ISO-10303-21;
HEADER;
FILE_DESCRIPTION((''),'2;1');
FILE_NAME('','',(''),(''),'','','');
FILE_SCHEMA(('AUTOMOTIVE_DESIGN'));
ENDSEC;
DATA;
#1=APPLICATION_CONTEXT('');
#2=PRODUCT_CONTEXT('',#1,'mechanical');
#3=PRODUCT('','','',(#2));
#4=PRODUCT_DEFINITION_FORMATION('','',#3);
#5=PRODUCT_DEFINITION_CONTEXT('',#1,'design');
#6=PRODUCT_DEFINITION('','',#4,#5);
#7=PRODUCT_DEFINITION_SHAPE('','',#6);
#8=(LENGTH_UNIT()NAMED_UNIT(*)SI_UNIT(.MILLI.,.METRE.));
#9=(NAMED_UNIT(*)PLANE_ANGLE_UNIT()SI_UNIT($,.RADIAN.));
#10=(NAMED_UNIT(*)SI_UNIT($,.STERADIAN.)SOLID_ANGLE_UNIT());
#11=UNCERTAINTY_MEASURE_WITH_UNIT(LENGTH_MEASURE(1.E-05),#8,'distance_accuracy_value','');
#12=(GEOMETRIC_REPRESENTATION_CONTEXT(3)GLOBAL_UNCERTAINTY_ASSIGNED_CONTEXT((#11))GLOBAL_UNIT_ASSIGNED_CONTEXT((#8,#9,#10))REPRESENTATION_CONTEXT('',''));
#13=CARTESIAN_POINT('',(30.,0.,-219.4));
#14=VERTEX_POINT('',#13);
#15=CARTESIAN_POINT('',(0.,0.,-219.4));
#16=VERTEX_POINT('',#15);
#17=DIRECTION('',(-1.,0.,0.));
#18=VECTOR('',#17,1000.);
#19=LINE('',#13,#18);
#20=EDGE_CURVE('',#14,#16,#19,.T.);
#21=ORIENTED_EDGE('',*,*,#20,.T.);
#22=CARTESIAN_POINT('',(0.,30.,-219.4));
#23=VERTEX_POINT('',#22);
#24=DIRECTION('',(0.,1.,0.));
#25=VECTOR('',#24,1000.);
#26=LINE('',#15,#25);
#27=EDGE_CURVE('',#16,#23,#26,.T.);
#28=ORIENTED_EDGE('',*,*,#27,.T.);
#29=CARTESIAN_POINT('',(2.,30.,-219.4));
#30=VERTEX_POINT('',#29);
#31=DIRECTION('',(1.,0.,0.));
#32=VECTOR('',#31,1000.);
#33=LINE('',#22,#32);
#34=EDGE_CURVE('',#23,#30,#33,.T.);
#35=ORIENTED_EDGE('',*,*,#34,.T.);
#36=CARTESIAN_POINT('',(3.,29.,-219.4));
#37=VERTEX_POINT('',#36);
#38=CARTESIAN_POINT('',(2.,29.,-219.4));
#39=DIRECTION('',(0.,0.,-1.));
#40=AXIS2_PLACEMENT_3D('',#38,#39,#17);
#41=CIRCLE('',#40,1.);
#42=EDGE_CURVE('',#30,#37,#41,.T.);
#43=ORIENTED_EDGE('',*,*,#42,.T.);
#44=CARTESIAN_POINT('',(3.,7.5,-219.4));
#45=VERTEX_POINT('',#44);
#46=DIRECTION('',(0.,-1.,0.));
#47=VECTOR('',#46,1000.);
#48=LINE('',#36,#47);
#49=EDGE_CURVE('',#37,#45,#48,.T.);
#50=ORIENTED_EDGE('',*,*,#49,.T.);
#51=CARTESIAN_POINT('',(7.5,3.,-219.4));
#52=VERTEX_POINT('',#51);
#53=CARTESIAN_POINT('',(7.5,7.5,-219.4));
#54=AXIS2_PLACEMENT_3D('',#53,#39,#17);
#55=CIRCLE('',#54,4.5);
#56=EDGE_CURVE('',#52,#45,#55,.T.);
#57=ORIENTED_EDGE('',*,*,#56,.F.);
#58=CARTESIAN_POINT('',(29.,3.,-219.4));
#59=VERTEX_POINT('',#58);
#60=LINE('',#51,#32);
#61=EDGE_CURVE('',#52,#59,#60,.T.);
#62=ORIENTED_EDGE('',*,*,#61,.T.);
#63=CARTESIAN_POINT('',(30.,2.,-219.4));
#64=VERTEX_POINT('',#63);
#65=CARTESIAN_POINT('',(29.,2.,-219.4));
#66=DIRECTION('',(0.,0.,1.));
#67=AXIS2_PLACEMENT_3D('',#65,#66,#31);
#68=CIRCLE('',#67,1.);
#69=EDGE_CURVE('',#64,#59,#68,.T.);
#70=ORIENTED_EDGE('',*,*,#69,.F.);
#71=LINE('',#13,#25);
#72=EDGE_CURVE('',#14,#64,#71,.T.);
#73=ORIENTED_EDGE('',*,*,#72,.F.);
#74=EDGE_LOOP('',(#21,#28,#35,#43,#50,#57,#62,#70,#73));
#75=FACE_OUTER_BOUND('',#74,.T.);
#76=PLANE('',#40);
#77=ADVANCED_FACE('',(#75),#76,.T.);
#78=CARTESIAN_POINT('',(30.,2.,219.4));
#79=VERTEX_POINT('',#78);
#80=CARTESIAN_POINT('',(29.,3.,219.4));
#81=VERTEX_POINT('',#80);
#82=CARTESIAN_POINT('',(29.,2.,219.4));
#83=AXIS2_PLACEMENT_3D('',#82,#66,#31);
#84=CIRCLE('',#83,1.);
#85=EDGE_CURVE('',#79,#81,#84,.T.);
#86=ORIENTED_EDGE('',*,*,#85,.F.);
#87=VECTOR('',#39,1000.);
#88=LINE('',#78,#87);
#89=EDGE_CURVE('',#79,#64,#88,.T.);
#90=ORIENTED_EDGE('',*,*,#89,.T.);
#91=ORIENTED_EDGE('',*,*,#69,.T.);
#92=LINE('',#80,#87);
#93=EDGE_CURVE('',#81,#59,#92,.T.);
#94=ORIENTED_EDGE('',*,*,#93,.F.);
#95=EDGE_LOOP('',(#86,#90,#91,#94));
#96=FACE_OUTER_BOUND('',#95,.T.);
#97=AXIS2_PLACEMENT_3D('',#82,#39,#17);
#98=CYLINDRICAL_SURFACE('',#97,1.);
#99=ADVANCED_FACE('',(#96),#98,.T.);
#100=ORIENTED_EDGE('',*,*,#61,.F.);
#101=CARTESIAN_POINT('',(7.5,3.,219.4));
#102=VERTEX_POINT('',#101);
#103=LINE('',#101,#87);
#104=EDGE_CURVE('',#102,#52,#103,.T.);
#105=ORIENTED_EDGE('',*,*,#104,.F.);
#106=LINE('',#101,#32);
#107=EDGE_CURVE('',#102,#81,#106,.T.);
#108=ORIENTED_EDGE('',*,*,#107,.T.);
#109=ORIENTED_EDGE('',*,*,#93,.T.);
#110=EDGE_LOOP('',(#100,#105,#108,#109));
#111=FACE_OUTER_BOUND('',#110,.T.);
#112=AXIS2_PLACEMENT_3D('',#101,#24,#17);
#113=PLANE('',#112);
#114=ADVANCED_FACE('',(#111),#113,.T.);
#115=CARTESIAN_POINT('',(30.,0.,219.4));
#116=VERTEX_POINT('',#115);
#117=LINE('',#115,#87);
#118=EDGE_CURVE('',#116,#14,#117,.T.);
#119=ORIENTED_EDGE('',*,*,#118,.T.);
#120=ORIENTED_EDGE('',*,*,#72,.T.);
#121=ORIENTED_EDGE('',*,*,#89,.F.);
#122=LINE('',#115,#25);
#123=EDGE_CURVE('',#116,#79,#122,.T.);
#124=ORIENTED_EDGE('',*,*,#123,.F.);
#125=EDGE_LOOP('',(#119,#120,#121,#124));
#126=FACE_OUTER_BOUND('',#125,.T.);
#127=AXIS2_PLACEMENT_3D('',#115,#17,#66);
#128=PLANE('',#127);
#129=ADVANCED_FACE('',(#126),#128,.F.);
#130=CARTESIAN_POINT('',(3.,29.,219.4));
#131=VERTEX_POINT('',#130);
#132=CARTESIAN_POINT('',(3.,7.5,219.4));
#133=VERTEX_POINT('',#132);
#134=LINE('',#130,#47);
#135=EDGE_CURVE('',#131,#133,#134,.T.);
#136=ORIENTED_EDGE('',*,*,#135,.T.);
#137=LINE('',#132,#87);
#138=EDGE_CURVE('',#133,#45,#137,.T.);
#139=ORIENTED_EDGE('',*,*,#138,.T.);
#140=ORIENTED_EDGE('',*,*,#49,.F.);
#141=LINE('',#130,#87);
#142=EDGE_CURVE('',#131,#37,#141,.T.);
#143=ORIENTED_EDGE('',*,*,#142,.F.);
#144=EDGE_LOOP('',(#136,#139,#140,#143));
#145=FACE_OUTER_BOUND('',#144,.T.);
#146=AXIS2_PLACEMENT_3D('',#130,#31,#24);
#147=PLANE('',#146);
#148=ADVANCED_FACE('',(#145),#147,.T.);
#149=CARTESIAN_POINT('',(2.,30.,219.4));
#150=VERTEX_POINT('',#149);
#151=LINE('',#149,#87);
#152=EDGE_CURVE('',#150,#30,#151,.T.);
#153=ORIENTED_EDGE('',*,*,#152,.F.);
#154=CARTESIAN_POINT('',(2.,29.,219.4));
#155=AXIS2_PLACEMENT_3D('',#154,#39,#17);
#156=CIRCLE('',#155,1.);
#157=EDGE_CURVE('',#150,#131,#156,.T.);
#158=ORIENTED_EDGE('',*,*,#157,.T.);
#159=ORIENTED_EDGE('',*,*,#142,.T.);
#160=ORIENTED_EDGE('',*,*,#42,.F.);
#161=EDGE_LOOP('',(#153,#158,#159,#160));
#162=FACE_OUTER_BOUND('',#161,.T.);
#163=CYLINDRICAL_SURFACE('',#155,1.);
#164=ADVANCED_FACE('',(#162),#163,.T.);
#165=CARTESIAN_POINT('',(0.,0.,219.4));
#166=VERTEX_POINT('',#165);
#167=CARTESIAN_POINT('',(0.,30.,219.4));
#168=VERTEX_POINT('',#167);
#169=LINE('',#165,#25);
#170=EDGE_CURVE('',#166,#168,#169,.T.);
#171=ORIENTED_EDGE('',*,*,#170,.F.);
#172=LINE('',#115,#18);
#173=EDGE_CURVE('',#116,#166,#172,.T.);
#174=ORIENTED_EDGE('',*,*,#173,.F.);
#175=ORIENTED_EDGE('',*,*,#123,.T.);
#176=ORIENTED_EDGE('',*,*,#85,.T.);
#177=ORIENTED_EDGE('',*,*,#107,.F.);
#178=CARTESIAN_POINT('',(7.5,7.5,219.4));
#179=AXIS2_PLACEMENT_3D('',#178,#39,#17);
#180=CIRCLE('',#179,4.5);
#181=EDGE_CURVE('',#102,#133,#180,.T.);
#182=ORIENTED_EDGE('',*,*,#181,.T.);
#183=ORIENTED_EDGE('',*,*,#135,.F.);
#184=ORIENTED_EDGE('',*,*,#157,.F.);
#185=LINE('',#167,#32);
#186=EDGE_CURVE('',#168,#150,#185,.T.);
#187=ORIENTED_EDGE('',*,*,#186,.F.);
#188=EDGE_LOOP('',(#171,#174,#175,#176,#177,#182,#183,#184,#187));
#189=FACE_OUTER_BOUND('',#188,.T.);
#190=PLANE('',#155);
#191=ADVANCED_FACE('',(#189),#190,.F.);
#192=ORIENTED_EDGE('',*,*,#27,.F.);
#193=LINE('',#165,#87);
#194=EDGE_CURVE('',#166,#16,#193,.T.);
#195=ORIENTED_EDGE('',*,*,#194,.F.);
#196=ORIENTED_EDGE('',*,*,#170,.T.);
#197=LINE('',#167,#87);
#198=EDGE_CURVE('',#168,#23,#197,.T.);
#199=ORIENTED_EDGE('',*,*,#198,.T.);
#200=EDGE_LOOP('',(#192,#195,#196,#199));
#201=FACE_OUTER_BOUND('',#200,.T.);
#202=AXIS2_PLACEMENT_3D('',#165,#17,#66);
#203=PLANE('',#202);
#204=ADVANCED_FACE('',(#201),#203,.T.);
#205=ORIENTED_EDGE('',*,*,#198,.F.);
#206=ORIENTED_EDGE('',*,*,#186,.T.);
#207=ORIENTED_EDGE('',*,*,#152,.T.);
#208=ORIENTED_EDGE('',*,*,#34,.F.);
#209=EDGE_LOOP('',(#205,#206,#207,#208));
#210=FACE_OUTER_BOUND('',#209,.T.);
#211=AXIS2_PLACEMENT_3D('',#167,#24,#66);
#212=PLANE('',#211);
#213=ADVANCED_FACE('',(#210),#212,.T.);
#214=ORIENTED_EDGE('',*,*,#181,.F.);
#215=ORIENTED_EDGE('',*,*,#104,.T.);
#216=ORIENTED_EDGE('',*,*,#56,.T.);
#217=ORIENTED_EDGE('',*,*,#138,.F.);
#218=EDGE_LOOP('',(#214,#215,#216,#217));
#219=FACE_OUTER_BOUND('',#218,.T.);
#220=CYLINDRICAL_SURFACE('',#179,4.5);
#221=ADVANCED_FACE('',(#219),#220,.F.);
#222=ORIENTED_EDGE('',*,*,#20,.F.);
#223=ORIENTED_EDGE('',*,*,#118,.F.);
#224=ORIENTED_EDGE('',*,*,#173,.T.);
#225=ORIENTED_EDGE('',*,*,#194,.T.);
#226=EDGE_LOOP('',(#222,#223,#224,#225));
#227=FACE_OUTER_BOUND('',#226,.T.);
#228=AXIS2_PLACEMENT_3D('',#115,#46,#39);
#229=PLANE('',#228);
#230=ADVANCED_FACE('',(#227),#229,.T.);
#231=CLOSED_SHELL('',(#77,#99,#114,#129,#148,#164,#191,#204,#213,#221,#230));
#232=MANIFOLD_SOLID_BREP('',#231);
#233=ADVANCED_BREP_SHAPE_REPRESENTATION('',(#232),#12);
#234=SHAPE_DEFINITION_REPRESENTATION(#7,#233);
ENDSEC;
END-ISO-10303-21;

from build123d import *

# Parameters (mm, degrees)
BOSS_EXTRUDE1_DEPTH = 219.4


with BuildPart() as part:
    # Sketch1 → Boss-Extrude1 (new, symmetric)
    with BuildSketch(Plane.XY):
        with BuildLine():
            Line((0, 0), (0, 30))
            Line((0, 30), (2, 30))
            ThreePointArc((2, 30), (2.707106781, 29.707106781), (3, 29))
            Line((3, 29), (3, 7.5))
            ThreePointArc((3, 7.5), (4.318019485, 4.318019485), (7.5, 3))
            Line((7.5, 3), (29, 3))
            ThreePointArc((29, 3), (29.707106781, 2.707106781), (30, 2))
            Line((30, 2), (30, 0))
            Line((30, 0), (0, 0))
        make_face()
    extrude(amount=BOSS_EXTRUDE1_DEPTH, both=True)


solid = part.part
